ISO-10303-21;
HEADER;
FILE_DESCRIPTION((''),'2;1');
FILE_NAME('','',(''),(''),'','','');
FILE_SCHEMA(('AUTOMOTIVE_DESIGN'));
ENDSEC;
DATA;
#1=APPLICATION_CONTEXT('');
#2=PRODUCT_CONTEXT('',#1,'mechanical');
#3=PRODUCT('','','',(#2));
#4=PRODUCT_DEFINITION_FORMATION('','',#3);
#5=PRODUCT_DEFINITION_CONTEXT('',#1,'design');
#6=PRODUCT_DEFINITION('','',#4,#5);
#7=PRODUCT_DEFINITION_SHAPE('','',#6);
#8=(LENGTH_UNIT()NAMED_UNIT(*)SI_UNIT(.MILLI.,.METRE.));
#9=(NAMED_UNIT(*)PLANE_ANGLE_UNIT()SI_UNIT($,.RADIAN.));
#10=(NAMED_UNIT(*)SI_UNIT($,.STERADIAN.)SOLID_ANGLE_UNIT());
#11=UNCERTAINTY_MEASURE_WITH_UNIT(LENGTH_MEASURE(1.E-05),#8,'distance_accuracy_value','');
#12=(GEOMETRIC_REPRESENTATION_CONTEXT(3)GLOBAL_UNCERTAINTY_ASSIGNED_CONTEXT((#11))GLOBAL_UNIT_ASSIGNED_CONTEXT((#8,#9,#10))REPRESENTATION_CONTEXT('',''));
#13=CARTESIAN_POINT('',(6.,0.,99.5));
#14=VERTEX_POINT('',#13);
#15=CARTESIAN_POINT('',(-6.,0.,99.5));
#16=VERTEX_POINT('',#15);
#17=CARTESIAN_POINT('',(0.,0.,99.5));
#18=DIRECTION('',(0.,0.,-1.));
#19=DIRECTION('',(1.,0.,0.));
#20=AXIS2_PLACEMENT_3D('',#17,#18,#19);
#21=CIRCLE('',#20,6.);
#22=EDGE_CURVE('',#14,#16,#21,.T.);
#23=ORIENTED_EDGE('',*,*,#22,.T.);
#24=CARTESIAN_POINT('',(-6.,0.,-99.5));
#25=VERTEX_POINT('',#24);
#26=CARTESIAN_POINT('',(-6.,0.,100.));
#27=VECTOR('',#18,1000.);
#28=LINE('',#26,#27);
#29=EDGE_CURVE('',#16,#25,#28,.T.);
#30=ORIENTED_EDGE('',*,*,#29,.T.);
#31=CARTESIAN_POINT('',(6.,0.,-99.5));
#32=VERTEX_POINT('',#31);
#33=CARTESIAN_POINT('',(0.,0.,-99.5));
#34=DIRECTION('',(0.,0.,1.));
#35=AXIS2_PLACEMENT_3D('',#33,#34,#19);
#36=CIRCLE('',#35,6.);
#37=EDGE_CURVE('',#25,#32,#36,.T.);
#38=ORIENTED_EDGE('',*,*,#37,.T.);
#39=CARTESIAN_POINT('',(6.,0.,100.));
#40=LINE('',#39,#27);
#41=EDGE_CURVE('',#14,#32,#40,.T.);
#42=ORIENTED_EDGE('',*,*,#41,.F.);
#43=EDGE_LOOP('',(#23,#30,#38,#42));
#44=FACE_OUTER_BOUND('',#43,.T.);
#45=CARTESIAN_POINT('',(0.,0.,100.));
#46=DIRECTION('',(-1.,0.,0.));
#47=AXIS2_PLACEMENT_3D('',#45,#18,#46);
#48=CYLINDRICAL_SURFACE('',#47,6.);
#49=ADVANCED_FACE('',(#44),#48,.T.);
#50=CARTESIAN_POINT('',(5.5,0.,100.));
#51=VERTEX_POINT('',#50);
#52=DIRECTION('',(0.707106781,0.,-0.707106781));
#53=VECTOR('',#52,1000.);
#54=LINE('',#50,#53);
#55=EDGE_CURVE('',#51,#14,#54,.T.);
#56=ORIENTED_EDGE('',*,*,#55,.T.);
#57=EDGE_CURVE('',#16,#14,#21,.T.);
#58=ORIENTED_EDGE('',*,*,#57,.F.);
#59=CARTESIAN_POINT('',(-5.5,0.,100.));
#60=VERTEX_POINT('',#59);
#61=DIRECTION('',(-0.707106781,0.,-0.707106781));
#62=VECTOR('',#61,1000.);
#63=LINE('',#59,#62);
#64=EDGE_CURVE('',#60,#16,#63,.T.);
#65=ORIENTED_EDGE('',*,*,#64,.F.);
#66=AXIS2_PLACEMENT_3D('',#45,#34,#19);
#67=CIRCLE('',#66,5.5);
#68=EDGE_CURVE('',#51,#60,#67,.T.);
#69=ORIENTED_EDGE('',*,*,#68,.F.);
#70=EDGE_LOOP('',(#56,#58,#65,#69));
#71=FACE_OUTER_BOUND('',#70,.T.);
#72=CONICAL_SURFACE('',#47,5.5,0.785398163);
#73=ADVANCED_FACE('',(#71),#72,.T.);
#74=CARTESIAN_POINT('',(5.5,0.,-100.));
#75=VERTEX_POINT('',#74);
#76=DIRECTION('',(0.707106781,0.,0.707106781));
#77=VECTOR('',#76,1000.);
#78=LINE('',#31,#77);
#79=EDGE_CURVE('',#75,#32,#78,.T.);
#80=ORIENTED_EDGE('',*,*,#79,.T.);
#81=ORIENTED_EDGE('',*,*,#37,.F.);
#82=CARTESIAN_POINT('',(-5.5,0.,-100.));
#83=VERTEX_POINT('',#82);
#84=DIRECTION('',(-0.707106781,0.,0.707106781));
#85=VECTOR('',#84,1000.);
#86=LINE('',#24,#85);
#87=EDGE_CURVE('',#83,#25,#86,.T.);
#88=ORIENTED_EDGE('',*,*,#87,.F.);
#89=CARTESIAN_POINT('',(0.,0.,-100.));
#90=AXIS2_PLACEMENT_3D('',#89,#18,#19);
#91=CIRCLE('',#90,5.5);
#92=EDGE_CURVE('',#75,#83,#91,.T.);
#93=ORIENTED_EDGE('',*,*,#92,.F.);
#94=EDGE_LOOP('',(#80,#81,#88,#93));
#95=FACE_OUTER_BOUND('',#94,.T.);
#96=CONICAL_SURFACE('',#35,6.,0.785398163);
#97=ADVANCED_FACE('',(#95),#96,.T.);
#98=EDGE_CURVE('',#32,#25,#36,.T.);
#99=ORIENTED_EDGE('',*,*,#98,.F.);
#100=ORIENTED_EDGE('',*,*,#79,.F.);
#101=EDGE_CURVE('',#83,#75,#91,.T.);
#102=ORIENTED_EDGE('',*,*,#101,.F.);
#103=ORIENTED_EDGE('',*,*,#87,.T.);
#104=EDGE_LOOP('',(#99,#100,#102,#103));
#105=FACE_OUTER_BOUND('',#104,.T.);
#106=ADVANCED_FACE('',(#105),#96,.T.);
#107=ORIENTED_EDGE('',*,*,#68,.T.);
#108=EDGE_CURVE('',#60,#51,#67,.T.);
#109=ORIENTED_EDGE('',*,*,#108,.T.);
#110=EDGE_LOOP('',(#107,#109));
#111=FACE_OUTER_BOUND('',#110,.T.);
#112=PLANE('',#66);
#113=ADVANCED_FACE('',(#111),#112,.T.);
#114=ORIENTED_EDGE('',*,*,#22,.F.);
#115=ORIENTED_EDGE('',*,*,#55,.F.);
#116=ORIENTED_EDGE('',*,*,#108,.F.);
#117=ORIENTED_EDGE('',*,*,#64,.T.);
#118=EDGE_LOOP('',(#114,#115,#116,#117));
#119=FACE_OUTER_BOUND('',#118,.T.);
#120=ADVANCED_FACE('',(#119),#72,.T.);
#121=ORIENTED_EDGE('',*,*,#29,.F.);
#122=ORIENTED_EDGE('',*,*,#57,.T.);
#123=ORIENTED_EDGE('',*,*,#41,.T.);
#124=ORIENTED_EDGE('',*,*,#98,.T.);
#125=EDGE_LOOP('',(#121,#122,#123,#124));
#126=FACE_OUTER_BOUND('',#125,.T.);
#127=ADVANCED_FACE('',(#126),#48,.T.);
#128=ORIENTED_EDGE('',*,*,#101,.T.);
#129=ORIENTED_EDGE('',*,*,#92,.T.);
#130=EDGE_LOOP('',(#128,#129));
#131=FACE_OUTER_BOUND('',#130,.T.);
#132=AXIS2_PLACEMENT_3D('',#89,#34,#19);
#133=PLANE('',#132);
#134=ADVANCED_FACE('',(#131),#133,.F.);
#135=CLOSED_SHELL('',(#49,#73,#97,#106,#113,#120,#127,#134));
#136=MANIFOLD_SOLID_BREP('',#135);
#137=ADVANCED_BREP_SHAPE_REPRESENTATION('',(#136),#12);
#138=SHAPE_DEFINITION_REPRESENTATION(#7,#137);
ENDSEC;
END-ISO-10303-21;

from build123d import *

# Parameters (mm, degrees)
SKETCH_1_R      = 6
EXTRUDE_1_DEPTH = 100
CHAMFER_1_SIZE  = 0.5


with BuildPart() as part:
    # 草图1 → 凸台-拉伸1 (new, symmetric)
    with BuildSketch(Plane.XY):
        Circle(SKETCH_1_R)
    extrude(amount=EXTRUDE_1_DEPTH, both=True)

    # 倒角1
    chamfer_1_edges = [part.edges().sort_by_distance(p)[0] for p in [
        (-6, 0, -100),
        (-6, 0, 100),
    ]]
    chamfer(chamfer_1_edges, length=CHAMFER_1_SIZE)


solid = part.part
